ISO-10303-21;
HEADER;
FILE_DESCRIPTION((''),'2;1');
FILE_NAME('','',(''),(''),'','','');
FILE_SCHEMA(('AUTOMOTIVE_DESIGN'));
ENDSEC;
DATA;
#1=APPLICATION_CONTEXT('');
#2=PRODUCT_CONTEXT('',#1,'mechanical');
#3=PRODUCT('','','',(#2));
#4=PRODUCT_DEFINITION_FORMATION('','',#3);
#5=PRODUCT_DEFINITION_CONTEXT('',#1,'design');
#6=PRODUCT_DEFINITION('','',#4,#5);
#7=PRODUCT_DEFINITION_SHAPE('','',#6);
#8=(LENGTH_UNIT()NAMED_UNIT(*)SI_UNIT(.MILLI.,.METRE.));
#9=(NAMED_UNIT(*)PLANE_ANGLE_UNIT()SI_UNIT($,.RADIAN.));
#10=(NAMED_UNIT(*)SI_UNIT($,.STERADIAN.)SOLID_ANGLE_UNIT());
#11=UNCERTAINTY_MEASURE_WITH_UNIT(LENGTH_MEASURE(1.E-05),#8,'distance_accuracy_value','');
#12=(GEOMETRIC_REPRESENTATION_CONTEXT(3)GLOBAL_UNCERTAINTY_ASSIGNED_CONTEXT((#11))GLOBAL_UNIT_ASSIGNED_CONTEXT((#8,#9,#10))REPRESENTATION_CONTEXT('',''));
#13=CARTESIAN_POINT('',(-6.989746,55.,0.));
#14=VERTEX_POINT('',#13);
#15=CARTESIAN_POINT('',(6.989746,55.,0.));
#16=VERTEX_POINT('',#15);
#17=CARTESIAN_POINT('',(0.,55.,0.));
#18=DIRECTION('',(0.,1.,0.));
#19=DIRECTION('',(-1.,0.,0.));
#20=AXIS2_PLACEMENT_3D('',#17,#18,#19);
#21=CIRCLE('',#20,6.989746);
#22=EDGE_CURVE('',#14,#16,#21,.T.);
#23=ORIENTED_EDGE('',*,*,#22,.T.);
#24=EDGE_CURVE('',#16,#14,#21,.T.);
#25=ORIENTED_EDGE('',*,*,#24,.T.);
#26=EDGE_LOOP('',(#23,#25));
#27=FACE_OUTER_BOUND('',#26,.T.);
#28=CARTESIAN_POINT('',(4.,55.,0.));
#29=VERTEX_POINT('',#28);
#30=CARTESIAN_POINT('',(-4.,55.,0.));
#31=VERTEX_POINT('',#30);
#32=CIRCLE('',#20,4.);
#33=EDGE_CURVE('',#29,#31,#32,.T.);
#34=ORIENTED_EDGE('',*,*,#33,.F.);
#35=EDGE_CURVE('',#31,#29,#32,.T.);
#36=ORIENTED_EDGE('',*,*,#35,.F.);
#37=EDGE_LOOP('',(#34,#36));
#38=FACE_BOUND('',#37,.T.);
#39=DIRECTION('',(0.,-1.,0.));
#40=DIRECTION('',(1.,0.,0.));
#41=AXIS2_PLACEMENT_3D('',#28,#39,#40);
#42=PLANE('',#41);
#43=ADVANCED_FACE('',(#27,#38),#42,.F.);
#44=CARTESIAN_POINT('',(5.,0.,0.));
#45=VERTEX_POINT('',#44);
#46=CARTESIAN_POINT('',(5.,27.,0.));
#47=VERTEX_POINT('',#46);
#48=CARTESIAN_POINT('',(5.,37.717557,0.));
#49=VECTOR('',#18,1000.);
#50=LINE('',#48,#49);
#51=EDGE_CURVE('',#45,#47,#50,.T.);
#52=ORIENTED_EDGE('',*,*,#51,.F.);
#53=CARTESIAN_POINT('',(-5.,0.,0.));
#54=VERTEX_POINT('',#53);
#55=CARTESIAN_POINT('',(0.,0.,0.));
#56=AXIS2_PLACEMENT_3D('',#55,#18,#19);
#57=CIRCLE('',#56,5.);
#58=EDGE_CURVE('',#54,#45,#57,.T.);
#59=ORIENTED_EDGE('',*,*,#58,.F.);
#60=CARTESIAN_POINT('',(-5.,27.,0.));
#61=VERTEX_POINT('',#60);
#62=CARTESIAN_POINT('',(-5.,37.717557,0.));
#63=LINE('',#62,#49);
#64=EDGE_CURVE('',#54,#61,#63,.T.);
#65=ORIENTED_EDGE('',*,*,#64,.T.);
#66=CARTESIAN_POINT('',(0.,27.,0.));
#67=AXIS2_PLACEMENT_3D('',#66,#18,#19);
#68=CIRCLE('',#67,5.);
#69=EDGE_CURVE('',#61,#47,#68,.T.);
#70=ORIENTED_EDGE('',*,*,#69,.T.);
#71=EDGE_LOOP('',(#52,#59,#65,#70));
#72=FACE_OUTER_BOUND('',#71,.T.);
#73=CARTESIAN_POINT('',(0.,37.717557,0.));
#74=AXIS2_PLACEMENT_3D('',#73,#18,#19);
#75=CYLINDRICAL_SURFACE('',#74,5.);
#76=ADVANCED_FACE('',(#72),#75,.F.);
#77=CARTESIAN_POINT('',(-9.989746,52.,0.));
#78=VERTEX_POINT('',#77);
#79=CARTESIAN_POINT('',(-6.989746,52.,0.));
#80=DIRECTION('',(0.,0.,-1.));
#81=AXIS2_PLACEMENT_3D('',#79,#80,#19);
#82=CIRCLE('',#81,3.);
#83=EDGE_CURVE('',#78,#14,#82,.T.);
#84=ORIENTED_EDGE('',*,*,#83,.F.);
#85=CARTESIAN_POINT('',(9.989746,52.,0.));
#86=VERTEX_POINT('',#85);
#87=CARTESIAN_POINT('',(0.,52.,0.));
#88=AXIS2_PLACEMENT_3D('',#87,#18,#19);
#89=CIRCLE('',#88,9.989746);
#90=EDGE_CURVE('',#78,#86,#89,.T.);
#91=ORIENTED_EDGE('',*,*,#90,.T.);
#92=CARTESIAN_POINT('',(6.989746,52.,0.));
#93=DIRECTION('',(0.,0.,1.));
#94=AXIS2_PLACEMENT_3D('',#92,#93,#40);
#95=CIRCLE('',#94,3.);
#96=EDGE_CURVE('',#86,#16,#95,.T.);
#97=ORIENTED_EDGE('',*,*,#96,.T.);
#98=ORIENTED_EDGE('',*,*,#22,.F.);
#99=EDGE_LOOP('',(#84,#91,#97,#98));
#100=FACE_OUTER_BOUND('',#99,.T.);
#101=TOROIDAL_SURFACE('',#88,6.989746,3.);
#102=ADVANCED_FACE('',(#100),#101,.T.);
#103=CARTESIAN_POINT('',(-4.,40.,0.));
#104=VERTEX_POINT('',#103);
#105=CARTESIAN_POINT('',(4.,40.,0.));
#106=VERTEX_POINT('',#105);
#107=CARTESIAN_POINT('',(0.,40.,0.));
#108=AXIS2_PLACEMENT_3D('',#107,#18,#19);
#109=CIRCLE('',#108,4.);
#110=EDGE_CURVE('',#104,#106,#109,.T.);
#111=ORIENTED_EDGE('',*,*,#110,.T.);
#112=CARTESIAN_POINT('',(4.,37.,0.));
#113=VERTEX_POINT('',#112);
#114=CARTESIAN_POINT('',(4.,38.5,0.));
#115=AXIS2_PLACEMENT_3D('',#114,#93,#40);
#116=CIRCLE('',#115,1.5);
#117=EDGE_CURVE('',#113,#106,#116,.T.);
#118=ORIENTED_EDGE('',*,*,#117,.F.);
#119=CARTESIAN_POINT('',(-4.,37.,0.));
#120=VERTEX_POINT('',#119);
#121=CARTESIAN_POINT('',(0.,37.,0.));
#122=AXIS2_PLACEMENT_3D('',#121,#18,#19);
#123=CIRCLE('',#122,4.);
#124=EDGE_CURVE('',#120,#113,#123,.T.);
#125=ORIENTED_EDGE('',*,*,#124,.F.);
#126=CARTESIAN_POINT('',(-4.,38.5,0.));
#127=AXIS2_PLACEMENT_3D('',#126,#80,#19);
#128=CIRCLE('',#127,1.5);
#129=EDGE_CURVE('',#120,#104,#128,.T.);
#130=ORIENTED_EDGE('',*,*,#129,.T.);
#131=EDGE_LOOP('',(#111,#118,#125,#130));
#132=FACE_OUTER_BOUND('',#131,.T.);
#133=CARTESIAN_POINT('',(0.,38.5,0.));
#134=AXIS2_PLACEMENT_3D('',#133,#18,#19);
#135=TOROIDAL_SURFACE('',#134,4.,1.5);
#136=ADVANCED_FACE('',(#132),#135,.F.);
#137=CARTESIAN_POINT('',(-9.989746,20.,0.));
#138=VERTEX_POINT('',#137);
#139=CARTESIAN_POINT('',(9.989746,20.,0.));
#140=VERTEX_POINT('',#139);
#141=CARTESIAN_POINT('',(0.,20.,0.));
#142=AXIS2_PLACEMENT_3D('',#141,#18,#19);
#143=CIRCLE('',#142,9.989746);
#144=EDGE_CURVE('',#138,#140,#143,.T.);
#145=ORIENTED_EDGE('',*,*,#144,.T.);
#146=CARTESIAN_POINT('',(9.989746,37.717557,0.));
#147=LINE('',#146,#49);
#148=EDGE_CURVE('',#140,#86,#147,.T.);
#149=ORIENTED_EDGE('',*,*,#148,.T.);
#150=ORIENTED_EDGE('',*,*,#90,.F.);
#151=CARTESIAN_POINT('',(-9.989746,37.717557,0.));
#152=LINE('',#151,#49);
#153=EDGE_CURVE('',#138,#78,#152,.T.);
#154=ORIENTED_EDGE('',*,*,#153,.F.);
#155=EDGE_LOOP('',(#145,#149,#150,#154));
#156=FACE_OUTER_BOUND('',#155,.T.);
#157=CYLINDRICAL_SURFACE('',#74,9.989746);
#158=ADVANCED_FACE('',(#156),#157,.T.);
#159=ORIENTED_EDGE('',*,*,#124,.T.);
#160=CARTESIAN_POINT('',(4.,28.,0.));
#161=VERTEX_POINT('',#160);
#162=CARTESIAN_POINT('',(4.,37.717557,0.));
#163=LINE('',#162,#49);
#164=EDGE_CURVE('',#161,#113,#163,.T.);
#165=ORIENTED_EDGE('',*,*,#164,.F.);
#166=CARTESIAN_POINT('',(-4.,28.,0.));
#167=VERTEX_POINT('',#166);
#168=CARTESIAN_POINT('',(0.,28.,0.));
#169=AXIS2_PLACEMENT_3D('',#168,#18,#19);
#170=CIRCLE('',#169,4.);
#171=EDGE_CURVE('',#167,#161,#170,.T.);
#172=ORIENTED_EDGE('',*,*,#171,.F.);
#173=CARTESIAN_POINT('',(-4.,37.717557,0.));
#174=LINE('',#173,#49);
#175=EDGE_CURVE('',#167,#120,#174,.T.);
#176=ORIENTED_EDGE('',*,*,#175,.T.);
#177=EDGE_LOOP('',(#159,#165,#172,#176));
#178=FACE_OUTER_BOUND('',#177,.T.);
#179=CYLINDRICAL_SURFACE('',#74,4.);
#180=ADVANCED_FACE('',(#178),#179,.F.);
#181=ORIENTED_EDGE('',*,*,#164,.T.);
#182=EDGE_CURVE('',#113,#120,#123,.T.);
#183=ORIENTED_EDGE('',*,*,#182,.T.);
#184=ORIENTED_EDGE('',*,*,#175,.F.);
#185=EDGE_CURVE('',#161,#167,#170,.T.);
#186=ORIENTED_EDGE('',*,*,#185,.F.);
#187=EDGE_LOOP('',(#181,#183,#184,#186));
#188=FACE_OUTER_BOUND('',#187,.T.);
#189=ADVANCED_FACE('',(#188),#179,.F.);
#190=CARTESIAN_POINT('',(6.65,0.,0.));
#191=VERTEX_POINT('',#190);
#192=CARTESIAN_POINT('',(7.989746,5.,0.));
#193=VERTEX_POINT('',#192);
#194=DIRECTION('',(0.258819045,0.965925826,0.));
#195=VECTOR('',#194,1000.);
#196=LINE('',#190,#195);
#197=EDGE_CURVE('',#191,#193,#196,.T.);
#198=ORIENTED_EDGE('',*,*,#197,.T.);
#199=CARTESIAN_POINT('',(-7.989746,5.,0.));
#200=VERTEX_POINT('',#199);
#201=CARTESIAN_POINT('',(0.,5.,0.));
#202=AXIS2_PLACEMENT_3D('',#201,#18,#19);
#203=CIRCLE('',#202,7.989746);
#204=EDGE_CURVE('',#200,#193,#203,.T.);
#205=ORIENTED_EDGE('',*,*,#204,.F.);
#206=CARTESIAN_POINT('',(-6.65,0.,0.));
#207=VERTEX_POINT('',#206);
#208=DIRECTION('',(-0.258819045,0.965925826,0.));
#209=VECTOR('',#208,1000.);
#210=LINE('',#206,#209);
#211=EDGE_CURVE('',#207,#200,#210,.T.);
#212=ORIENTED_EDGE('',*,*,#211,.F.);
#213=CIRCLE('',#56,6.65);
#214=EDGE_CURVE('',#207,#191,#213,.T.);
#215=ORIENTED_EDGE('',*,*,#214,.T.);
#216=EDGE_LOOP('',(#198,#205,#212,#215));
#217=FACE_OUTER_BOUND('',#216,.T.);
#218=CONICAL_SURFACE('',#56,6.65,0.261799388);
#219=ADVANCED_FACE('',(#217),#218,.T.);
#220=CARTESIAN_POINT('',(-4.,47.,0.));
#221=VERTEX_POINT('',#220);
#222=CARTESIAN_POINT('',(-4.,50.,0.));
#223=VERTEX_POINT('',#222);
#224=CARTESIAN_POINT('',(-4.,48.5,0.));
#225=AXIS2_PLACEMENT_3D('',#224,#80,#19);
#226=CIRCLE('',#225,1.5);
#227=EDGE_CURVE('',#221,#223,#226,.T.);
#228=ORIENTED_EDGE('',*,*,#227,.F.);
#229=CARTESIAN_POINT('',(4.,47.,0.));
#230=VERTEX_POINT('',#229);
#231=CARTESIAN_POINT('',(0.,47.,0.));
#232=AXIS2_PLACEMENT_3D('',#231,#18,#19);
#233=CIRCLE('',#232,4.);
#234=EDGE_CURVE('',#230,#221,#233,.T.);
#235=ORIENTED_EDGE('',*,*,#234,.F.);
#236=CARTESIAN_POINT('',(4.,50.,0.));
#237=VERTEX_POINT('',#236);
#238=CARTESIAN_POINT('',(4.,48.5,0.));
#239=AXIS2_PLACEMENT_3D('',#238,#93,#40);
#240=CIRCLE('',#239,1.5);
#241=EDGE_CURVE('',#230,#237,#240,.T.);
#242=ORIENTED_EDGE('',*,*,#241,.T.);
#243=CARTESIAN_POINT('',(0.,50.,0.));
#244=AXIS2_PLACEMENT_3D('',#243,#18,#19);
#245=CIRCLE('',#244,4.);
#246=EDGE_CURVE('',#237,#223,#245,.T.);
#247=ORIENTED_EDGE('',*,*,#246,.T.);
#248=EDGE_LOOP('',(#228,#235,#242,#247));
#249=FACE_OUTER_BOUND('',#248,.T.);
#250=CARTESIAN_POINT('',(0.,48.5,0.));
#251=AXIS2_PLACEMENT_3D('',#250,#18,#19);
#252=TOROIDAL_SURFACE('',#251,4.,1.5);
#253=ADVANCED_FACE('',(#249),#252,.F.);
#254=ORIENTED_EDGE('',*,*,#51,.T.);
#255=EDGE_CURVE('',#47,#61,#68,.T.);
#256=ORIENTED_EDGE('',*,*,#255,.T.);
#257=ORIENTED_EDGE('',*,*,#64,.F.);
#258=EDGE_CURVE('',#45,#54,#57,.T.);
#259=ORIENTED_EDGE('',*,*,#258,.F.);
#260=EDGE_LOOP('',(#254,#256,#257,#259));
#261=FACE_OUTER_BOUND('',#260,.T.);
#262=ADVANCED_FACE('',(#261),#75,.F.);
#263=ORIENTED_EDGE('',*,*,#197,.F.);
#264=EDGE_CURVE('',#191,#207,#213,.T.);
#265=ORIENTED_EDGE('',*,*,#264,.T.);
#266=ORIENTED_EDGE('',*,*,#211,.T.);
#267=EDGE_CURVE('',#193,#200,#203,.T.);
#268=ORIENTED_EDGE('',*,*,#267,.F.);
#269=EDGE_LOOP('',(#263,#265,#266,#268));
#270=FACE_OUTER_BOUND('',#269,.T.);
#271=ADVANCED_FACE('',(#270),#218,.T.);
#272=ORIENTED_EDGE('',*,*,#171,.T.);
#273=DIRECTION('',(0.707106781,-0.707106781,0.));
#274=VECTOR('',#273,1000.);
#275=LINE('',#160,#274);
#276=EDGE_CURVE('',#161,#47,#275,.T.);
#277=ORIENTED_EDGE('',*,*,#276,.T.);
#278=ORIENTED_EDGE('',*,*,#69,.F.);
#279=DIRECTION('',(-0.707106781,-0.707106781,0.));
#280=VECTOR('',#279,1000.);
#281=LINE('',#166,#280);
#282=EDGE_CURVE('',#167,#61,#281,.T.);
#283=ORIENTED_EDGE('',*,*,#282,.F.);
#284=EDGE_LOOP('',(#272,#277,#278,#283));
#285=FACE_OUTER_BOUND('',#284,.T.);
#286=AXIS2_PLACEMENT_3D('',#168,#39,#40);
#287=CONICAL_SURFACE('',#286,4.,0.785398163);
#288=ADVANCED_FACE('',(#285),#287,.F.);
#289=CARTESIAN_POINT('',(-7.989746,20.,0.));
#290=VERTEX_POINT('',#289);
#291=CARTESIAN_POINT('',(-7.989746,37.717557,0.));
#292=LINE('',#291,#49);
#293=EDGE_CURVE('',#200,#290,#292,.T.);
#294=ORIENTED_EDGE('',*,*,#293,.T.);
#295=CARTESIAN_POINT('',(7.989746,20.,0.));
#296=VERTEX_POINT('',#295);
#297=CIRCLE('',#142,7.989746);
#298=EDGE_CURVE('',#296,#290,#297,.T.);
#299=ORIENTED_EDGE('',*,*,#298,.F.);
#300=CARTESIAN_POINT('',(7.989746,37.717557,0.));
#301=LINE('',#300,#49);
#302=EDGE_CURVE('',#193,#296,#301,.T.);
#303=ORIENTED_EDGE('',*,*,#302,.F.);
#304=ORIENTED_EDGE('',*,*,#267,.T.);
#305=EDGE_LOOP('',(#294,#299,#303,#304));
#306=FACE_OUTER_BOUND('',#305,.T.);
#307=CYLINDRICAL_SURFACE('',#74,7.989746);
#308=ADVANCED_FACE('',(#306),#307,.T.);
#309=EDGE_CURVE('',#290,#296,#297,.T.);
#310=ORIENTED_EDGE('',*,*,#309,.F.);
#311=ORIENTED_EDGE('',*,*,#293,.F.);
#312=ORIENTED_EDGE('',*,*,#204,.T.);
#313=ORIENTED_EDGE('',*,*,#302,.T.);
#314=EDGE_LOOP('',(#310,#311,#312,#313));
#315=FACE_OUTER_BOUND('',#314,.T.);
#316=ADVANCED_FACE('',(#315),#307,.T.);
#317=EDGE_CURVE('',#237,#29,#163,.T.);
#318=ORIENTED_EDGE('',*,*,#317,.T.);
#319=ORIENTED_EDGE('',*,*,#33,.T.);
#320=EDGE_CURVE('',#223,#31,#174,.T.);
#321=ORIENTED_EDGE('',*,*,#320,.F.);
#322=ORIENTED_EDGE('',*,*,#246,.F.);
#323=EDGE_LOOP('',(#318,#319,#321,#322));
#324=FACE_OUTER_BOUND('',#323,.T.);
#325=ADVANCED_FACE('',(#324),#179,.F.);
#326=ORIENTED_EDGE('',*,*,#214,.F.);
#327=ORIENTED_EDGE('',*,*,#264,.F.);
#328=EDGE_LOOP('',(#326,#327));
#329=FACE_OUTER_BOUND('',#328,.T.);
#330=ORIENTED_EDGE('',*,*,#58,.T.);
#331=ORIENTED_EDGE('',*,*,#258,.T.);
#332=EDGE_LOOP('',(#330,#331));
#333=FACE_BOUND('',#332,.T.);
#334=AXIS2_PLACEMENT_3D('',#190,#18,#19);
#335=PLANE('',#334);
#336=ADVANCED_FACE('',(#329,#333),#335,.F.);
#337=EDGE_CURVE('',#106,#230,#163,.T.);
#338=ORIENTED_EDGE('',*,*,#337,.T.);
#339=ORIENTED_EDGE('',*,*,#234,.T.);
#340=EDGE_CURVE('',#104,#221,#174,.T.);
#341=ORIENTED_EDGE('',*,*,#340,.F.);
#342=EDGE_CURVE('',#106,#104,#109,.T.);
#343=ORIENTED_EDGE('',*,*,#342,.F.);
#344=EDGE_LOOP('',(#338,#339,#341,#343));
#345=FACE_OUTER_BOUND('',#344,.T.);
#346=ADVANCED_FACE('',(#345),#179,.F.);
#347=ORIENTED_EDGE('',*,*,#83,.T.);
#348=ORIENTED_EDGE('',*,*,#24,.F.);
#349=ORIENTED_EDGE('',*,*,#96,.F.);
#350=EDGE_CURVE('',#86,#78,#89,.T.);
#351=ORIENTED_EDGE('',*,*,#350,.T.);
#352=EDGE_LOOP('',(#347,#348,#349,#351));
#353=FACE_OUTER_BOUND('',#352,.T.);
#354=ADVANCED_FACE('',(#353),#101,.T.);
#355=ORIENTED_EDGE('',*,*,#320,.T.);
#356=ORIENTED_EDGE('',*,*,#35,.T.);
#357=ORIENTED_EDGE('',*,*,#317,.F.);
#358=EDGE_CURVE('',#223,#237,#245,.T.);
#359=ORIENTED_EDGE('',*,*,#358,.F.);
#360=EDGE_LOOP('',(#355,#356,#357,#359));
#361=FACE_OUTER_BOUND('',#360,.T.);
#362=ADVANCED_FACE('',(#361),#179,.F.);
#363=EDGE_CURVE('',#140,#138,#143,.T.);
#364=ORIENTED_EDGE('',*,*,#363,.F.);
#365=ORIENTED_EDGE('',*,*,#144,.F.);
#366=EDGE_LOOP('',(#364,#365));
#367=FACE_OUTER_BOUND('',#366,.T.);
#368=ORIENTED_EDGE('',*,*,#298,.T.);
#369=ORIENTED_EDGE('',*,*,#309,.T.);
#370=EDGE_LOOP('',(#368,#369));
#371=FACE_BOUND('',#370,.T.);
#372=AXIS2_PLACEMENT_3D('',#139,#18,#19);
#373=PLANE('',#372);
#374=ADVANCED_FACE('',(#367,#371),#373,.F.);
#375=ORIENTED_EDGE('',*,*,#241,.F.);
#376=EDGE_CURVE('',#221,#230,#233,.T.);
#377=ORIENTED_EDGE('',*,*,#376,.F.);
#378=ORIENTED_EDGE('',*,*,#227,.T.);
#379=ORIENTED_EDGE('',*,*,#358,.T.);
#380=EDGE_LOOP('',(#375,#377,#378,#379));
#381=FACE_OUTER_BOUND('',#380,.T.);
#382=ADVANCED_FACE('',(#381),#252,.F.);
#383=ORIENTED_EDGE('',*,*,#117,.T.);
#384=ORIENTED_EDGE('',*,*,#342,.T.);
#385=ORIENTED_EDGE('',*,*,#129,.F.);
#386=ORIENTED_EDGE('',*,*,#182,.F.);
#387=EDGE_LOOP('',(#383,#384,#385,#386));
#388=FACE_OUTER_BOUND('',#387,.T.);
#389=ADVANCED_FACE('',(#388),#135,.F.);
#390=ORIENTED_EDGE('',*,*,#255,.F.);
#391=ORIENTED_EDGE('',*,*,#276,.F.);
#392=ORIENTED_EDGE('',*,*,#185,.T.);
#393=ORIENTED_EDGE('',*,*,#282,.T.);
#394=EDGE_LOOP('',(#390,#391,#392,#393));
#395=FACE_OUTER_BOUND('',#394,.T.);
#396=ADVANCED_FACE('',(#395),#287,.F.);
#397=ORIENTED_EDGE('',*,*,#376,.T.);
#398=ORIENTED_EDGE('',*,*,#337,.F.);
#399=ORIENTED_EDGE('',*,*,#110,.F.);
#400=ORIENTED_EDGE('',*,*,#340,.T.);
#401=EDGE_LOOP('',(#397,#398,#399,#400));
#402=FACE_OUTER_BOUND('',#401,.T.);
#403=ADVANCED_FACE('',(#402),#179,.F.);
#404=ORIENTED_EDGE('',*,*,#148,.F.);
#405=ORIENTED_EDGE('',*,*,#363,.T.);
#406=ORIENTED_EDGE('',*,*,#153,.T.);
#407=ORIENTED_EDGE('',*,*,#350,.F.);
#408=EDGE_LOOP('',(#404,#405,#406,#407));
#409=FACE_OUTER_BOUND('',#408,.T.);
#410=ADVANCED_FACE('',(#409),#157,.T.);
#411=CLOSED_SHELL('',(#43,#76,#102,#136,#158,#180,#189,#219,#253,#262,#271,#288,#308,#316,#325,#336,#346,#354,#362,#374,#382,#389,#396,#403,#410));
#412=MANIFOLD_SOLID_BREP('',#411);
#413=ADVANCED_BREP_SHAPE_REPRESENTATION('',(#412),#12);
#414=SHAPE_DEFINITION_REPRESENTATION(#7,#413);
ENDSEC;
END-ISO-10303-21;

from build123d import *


with BuildPart() as part:
    # Pin Profile Sketch → Pin Body Revolve (revolve)
    with BuildSketch(Plane.XY, mode=Mode.PRIVATE) as pin_body_revolve_sk:
        with BuildLine():
            Line((5, 0), (5, 27))
            Line((5, 27), (4, 28))
            Line((4, 28), (4, 37))
            ThreePointArc((4, 37), (5.5, 38.5), (4, 40))
            Line((4, 40), (4, 47))
            ThreePointArc((4, 47), (5.5, 48.5), (4, 50))
            Line((4, 50), (4, 55))
            Line((4, 55), (6.989745962, 55))
            ThreePointArc((6.989745962, 55), (9.111066306, 54.121320344), (9.989745962, 52))
            Line((9.989745962, 52), (9.989745962, 20))
            Line((9.989745962, 20), (7.989745962, 20))
            Line((7.989745962, 20), (7.989745962, 5))
            Line((7.989745962, 5), (6.65, 0))
            Line((6.65, 0), (5, 0))
        make_face()
    revolve(pin_body_revolve_sk.sketch.rotate(Axis((0, 37.717557252, 0), (0, -1, 0)), 180), axis=Axis((0, 37.717557252, 0), (0, -1, 0)))


solid = part.part
